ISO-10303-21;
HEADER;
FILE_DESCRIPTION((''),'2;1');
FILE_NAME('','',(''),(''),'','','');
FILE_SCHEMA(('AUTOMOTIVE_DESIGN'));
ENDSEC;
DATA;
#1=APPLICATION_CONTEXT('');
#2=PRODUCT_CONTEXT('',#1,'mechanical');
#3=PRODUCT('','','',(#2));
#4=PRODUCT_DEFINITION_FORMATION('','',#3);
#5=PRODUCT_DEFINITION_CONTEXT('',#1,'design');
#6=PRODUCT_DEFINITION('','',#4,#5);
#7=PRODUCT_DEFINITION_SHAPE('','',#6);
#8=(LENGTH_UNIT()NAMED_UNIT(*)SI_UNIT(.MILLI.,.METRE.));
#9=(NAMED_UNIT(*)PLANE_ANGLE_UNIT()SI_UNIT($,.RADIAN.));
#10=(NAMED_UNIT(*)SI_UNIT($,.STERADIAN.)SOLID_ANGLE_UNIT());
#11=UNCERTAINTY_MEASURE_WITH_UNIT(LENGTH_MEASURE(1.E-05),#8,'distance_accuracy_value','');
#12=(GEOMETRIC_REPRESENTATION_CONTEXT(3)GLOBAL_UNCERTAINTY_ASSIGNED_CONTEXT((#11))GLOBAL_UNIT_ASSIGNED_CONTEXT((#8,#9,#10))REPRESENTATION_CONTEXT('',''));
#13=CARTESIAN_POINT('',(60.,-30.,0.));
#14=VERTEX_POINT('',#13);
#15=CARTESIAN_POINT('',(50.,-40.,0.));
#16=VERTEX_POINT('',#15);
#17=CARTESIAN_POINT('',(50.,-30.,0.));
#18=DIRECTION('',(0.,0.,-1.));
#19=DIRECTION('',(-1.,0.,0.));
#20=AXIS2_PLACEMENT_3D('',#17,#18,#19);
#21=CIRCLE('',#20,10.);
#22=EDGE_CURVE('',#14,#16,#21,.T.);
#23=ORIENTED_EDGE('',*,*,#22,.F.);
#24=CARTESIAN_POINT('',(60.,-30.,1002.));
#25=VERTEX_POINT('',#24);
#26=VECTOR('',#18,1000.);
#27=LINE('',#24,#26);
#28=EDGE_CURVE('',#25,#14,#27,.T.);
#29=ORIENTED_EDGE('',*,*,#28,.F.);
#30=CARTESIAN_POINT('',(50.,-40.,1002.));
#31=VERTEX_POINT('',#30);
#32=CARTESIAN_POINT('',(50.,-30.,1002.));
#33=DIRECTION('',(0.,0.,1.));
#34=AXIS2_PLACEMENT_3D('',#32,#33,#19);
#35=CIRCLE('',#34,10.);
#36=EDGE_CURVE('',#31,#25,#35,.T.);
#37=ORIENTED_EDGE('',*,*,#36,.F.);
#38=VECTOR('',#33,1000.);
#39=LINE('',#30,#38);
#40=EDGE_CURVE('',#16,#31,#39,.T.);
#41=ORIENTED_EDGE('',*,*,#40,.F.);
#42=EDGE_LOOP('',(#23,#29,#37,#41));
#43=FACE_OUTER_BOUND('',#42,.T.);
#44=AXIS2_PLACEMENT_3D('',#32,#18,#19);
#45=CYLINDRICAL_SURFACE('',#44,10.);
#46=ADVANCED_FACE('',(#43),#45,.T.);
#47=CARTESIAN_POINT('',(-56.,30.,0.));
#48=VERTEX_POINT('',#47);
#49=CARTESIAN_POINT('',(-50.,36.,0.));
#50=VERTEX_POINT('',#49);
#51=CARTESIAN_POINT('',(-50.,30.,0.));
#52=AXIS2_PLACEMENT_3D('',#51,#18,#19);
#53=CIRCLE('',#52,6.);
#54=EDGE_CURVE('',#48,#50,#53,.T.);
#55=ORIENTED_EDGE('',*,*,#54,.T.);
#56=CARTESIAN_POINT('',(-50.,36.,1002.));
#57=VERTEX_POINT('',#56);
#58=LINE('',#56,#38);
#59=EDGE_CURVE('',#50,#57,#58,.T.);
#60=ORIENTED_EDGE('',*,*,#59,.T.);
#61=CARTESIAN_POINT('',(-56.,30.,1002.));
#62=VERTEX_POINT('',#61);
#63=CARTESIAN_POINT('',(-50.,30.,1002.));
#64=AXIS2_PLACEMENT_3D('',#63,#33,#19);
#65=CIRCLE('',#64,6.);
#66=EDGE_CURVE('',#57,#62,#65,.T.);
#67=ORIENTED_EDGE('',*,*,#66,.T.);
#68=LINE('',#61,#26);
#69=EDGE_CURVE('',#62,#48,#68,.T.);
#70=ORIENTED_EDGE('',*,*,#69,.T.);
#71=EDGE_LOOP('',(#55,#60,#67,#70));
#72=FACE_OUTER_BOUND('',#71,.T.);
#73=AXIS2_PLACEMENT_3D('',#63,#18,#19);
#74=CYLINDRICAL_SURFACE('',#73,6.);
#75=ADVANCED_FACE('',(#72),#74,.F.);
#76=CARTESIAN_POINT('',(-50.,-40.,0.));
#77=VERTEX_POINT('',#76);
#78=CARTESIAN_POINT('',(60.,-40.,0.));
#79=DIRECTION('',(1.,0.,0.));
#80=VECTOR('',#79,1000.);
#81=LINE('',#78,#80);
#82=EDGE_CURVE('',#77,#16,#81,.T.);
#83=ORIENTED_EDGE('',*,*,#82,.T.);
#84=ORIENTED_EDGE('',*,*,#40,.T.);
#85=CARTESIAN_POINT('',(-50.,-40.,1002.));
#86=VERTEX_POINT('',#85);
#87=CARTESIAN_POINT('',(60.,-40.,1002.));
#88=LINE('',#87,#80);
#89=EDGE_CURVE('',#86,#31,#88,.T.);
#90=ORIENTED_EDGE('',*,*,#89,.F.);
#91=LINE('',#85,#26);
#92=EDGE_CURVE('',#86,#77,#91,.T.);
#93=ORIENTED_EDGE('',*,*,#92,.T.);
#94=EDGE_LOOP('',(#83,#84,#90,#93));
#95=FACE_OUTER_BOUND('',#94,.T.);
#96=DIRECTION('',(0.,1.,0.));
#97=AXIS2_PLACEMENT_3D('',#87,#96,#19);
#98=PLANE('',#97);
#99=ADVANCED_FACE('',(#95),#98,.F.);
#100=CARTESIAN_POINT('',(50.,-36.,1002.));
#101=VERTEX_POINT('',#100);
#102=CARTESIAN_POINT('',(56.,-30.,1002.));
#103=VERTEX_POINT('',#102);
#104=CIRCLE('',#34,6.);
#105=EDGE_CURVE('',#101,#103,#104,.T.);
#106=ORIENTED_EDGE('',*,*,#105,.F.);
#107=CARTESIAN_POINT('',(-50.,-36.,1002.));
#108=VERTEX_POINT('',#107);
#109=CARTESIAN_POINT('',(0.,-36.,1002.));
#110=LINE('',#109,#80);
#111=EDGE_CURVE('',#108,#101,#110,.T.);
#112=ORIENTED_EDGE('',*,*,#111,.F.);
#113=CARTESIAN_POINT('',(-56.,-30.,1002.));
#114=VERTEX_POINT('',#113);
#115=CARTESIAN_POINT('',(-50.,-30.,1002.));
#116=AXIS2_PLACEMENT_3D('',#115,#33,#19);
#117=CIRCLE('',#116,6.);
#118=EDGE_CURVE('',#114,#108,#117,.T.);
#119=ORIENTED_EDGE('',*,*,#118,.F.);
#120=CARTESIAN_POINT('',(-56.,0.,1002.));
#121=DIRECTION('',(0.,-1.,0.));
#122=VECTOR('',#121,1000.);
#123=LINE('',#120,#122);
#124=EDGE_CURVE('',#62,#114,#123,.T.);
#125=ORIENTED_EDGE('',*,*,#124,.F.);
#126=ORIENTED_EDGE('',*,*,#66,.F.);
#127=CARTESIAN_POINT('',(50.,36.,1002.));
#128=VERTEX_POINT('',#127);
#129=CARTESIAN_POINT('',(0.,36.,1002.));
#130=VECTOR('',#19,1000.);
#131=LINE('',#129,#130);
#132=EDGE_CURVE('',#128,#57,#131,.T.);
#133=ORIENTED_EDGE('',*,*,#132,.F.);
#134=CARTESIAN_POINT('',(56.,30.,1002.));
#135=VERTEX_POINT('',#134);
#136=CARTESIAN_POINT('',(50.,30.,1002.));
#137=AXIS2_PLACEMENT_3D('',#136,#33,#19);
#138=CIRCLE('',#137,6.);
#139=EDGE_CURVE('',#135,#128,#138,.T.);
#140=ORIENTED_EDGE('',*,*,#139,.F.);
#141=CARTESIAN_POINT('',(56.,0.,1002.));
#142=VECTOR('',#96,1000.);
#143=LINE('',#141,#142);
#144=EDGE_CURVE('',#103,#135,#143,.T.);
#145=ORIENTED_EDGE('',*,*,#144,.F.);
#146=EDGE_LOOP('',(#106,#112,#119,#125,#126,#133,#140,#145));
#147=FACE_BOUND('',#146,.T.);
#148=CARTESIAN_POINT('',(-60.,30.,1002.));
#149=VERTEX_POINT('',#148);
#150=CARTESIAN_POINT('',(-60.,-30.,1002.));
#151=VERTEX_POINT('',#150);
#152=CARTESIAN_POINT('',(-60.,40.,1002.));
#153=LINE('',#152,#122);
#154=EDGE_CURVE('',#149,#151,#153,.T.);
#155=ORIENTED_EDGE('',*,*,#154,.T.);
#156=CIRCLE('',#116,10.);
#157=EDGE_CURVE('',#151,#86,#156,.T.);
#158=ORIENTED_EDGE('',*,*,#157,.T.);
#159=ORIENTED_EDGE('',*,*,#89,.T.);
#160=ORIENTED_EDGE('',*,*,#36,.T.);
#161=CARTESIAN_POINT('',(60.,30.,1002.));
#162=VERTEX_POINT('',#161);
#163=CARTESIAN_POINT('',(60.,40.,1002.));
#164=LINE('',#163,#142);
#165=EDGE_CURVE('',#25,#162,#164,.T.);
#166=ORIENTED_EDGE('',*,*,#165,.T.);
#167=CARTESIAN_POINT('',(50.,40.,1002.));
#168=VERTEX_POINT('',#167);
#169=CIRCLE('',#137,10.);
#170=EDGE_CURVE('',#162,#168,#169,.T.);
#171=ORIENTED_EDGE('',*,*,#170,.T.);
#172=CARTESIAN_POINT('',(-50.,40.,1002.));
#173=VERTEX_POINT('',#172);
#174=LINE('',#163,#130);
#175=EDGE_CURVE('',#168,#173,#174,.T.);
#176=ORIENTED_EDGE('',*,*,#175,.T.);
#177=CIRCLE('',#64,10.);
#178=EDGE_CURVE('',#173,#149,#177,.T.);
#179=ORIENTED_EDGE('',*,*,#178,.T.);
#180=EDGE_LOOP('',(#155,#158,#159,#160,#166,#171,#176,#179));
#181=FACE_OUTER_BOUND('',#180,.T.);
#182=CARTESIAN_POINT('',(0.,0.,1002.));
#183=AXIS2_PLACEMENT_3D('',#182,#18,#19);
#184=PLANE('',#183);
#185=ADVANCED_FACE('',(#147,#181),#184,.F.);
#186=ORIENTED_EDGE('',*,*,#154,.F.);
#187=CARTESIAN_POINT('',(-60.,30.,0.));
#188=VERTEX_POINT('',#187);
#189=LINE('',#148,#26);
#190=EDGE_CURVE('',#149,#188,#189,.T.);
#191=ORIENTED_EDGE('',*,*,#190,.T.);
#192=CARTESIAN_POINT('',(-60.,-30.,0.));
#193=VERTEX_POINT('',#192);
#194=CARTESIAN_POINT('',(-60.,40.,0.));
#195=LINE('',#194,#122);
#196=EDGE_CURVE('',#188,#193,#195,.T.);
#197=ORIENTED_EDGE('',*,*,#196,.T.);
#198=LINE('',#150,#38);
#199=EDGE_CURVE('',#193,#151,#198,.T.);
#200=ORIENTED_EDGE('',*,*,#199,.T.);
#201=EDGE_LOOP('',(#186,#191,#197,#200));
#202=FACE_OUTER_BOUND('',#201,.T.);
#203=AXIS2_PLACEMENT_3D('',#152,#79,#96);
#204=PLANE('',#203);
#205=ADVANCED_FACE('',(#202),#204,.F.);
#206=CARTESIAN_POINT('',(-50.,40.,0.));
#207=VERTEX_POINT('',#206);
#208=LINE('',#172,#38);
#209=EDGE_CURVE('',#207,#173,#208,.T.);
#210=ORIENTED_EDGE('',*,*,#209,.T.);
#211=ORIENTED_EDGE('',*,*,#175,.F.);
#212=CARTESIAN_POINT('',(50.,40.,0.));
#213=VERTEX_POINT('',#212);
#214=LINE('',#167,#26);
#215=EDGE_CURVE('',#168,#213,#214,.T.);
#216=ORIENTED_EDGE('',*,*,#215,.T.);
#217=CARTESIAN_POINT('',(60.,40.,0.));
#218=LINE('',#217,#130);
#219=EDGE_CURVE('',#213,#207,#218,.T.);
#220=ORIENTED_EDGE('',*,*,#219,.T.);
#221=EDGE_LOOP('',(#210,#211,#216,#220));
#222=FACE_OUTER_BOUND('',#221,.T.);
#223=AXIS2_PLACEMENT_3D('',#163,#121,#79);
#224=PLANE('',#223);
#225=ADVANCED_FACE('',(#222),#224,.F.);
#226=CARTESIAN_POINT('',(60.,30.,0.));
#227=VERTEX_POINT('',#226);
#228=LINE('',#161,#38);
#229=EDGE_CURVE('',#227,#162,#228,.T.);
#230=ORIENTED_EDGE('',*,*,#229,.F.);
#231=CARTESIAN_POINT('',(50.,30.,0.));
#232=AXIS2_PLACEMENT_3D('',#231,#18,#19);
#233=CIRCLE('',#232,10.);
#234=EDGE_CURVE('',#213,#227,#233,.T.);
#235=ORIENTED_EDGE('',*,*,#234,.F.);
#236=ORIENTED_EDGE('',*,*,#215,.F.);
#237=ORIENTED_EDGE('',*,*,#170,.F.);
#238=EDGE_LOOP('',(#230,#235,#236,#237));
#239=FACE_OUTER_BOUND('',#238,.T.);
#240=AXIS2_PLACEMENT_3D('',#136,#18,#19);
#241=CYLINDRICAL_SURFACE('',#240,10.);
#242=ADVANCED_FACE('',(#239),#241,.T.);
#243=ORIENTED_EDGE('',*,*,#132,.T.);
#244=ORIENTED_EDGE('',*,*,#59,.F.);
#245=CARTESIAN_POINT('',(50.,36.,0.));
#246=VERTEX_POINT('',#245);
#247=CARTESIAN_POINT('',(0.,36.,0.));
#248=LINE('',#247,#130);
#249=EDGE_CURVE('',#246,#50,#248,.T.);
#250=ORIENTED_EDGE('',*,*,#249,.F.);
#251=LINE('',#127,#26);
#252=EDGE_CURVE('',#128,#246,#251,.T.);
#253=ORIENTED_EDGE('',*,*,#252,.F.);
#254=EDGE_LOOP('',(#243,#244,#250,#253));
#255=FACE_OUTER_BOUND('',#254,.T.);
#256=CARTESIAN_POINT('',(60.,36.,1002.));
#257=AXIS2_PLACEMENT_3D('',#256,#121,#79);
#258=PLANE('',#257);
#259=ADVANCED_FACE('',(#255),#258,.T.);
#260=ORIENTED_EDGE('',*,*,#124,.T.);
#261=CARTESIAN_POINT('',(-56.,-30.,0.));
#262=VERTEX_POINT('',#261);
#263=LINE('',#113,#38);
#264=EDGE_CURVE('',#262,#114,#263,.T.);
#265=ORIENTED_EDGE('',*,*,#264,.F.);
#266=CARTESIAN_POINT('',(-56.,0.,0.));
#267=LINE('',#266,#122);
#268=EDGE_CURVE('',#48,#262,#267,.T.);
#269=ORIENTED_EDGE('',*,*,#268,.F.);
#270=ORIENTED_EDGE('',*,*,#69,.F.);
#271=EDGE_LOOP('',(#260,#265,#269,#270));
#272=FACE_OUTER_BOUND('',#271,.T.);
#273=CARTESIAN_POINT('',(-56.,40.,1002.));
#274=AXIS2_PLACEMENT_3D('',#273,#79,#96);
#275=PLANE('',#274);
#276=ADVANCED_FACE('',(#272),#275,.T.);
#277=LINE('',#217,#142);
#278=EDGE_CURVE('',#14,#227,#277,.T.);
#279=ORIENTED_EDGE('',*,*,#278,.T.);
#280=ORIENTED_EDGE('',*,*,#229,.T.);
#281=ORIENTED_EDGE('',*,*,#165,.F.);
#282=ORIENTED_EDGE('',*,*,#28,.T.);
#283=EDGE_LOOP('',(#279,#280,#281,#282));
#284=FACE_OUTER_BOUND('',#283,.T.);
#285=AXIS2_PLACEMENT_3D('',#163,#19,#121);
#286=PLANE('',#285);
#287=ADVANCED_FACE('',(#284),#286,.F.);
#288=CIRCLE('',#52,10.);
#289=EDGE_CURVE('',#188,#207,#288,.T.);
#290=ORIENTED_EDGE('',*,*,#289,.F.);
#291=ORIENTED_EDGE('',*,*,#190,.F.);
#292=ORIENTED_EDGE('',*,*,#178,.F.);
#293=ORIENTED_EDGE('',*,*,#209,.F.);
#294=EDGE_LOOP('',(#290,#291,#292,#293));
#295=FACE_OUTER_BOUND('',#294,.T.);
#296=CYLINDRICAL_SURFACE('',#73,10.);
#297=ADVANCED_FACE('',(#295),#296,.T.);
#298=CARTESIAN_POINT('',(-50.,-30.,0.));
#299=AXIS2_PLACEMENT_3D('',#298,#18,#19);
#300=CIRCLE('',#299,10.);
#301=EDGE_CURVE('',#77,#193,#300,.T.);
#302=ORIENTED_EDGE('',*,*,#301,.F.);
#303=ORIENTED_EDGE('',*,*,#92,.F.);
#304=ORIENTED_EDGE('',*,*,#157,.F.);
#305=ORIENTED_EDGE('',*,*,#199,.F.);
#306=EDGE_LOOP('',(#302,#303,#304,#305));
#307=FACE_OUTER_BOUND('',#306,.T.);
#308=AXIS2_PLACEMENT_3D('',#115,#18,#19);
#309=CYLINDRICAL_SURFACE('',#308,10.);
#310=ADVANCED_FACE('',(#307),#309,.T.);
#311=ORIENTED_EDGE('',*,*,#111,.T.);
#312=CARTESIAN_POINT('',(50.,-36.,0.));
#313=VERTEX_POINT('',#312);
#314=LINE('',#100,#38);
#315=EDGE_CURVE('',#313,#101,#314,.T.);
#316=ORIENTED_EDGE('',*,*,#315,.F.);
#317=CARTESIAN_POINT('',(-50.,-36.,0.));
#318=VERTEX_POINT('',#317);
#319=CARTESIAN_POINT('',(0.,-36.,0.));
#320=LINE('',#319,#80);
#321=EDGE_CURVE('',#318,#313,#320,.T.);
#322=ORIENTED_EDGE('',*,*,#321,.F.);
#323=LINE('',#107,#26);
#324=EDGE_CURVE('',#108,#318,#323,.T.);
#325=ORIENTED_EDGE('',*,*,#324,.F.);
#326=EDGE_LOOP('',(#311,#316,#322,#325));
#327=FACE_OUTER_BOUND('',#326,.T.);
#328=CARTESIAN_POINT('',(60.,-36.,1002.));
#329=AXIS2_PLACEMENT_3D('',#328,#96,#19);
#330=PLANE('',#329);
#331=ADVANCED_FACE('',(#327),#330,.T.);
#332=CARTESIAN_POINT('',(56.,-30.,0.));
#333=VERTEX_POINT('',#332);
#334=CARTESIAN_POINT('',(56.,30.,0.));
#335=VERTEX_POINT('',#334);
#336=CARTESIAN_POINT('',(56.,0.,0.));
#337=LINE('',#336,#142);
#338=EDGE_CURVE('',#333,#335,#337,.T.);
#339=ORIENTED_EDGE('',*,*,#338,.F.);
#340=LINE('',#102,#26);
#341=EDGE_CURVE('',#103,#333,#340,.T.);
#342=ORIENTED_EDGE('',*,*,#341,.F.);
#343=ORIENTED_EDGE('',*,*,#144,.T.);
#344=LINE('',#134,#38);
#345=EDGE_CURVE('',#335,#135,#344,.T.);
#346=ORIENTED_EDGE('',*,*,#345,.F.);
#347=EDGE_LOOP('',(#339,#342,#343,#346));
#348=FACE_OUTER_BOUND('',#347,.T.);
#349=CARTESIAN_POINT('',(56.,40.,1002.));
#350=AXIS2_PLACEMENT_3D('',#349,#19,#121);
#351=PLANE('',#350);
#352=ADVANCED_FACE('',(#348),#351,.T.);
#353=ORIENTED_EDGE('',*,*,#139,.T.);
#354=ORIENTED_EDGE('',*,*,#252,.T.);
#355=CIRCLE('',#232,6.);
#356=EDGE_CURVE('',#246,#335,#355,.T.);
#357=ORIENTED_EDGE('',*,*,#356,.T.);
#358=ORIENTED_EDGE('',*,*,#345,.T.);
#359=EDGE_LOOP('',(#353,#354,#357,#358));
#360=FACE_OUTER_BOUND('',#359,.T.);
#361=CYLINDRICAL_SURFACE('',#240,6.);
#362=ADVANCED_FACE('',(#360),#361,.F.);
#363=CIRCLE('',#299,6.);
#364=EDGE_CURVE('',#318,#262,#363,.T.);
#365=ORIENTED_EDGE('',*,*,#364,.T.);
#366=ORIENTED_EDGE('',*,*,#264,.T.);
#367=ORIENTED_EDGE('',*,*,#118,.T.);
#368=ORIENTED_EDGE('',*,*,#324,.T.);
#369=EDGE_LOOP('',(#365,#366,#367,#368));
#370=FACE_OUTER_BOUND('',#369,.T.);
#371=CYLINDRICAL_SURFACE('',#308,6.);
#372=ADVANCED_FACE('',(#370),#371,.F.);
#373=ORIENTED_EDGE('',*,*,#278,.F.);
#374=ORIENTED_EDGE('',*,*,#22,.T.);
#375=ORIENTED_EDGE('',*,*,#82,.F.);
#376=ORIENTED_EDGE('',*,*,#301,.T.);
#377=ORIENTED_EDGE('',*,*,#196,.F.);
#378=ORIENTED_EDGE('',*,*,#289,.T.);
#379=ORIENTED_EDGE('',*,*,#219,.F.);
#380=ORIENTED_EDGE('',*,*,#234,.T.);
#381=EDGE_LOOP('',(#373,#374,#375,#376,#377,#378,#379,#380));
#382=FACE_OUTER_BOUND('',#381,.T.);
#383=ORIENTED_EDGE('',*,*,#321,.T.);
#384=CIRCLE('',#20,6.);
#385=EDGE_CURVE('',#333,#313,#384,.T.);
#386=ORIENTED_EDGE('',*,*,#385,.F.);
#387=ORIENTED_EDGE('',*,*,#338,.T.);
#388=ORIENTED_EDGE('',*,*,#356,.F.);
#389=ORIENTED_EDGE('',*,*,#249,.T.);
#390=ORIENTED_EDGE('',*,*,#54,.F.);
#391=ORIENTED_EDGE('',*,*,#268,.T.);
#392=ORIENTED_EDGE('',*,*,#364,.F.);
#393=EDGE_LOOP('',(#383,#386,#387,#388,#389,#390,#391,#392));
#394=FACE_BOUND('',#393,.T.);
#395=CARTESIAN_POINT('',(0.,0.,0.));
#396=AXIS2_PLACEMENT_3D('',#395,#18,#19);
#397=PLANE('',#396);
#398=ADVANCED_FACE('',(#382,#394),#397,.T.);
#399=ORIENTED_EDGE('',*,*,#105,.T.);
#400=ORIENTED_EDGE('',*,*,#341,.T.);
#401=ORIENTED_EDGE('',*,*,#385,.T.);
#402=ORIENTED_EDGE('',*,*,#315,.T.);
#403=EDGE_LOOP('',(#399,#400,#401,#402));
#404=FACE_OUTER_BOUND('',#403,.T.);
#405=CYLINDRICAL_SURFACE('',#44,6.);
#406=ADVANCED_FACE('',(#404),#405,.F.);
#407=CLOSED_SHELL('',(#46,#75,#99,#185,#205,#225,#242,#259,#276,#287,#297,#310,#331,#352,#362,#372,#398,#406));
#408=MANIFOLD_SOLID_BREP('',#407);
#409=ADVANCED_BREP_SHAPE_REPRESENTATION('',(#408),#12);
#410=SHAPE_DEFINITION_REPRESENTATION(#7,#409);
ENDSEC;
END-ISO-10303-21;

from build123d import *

# Parameters (mm, degrees)
SKETCH1_W           = 120
SKETCH1_H           = 80
BOSS_EXTRUDE1_DEPTH = 1002
FILLET1_R           = 10
SHELL1_T            = -4


with BuildPart() as part:
    # Sketch1 → Boss-Extrude1 (new body)
    with BuildSketch(Plane.XY):
        Rectangle(SKETCH1_W, SKETCH1_H)
    extrude(amount=BOSS_EXTRUDE1_DEPTH)

    # Fillet1
    fillet1_edges = [part.edges().sort_by_distance(p)[0] for p in [
        (-60, 40, 501),
        (60, 40, 501),
        (60, -40, 501),
        (-60, -40, 501),
    ]]
    fillet(fillet1_edges, radius=FILLET1_R)

    # Shell1
    shell1_openings = [part.faces().sort_by_distance(p)[0] for p in [
        (0, 0, 1002),
        (0, 0, 0),
    ]]
    offset(amount=SHELL1_T, openings=shell1_openings, kind=Kind.INTERSECTION)


solid = part.part
